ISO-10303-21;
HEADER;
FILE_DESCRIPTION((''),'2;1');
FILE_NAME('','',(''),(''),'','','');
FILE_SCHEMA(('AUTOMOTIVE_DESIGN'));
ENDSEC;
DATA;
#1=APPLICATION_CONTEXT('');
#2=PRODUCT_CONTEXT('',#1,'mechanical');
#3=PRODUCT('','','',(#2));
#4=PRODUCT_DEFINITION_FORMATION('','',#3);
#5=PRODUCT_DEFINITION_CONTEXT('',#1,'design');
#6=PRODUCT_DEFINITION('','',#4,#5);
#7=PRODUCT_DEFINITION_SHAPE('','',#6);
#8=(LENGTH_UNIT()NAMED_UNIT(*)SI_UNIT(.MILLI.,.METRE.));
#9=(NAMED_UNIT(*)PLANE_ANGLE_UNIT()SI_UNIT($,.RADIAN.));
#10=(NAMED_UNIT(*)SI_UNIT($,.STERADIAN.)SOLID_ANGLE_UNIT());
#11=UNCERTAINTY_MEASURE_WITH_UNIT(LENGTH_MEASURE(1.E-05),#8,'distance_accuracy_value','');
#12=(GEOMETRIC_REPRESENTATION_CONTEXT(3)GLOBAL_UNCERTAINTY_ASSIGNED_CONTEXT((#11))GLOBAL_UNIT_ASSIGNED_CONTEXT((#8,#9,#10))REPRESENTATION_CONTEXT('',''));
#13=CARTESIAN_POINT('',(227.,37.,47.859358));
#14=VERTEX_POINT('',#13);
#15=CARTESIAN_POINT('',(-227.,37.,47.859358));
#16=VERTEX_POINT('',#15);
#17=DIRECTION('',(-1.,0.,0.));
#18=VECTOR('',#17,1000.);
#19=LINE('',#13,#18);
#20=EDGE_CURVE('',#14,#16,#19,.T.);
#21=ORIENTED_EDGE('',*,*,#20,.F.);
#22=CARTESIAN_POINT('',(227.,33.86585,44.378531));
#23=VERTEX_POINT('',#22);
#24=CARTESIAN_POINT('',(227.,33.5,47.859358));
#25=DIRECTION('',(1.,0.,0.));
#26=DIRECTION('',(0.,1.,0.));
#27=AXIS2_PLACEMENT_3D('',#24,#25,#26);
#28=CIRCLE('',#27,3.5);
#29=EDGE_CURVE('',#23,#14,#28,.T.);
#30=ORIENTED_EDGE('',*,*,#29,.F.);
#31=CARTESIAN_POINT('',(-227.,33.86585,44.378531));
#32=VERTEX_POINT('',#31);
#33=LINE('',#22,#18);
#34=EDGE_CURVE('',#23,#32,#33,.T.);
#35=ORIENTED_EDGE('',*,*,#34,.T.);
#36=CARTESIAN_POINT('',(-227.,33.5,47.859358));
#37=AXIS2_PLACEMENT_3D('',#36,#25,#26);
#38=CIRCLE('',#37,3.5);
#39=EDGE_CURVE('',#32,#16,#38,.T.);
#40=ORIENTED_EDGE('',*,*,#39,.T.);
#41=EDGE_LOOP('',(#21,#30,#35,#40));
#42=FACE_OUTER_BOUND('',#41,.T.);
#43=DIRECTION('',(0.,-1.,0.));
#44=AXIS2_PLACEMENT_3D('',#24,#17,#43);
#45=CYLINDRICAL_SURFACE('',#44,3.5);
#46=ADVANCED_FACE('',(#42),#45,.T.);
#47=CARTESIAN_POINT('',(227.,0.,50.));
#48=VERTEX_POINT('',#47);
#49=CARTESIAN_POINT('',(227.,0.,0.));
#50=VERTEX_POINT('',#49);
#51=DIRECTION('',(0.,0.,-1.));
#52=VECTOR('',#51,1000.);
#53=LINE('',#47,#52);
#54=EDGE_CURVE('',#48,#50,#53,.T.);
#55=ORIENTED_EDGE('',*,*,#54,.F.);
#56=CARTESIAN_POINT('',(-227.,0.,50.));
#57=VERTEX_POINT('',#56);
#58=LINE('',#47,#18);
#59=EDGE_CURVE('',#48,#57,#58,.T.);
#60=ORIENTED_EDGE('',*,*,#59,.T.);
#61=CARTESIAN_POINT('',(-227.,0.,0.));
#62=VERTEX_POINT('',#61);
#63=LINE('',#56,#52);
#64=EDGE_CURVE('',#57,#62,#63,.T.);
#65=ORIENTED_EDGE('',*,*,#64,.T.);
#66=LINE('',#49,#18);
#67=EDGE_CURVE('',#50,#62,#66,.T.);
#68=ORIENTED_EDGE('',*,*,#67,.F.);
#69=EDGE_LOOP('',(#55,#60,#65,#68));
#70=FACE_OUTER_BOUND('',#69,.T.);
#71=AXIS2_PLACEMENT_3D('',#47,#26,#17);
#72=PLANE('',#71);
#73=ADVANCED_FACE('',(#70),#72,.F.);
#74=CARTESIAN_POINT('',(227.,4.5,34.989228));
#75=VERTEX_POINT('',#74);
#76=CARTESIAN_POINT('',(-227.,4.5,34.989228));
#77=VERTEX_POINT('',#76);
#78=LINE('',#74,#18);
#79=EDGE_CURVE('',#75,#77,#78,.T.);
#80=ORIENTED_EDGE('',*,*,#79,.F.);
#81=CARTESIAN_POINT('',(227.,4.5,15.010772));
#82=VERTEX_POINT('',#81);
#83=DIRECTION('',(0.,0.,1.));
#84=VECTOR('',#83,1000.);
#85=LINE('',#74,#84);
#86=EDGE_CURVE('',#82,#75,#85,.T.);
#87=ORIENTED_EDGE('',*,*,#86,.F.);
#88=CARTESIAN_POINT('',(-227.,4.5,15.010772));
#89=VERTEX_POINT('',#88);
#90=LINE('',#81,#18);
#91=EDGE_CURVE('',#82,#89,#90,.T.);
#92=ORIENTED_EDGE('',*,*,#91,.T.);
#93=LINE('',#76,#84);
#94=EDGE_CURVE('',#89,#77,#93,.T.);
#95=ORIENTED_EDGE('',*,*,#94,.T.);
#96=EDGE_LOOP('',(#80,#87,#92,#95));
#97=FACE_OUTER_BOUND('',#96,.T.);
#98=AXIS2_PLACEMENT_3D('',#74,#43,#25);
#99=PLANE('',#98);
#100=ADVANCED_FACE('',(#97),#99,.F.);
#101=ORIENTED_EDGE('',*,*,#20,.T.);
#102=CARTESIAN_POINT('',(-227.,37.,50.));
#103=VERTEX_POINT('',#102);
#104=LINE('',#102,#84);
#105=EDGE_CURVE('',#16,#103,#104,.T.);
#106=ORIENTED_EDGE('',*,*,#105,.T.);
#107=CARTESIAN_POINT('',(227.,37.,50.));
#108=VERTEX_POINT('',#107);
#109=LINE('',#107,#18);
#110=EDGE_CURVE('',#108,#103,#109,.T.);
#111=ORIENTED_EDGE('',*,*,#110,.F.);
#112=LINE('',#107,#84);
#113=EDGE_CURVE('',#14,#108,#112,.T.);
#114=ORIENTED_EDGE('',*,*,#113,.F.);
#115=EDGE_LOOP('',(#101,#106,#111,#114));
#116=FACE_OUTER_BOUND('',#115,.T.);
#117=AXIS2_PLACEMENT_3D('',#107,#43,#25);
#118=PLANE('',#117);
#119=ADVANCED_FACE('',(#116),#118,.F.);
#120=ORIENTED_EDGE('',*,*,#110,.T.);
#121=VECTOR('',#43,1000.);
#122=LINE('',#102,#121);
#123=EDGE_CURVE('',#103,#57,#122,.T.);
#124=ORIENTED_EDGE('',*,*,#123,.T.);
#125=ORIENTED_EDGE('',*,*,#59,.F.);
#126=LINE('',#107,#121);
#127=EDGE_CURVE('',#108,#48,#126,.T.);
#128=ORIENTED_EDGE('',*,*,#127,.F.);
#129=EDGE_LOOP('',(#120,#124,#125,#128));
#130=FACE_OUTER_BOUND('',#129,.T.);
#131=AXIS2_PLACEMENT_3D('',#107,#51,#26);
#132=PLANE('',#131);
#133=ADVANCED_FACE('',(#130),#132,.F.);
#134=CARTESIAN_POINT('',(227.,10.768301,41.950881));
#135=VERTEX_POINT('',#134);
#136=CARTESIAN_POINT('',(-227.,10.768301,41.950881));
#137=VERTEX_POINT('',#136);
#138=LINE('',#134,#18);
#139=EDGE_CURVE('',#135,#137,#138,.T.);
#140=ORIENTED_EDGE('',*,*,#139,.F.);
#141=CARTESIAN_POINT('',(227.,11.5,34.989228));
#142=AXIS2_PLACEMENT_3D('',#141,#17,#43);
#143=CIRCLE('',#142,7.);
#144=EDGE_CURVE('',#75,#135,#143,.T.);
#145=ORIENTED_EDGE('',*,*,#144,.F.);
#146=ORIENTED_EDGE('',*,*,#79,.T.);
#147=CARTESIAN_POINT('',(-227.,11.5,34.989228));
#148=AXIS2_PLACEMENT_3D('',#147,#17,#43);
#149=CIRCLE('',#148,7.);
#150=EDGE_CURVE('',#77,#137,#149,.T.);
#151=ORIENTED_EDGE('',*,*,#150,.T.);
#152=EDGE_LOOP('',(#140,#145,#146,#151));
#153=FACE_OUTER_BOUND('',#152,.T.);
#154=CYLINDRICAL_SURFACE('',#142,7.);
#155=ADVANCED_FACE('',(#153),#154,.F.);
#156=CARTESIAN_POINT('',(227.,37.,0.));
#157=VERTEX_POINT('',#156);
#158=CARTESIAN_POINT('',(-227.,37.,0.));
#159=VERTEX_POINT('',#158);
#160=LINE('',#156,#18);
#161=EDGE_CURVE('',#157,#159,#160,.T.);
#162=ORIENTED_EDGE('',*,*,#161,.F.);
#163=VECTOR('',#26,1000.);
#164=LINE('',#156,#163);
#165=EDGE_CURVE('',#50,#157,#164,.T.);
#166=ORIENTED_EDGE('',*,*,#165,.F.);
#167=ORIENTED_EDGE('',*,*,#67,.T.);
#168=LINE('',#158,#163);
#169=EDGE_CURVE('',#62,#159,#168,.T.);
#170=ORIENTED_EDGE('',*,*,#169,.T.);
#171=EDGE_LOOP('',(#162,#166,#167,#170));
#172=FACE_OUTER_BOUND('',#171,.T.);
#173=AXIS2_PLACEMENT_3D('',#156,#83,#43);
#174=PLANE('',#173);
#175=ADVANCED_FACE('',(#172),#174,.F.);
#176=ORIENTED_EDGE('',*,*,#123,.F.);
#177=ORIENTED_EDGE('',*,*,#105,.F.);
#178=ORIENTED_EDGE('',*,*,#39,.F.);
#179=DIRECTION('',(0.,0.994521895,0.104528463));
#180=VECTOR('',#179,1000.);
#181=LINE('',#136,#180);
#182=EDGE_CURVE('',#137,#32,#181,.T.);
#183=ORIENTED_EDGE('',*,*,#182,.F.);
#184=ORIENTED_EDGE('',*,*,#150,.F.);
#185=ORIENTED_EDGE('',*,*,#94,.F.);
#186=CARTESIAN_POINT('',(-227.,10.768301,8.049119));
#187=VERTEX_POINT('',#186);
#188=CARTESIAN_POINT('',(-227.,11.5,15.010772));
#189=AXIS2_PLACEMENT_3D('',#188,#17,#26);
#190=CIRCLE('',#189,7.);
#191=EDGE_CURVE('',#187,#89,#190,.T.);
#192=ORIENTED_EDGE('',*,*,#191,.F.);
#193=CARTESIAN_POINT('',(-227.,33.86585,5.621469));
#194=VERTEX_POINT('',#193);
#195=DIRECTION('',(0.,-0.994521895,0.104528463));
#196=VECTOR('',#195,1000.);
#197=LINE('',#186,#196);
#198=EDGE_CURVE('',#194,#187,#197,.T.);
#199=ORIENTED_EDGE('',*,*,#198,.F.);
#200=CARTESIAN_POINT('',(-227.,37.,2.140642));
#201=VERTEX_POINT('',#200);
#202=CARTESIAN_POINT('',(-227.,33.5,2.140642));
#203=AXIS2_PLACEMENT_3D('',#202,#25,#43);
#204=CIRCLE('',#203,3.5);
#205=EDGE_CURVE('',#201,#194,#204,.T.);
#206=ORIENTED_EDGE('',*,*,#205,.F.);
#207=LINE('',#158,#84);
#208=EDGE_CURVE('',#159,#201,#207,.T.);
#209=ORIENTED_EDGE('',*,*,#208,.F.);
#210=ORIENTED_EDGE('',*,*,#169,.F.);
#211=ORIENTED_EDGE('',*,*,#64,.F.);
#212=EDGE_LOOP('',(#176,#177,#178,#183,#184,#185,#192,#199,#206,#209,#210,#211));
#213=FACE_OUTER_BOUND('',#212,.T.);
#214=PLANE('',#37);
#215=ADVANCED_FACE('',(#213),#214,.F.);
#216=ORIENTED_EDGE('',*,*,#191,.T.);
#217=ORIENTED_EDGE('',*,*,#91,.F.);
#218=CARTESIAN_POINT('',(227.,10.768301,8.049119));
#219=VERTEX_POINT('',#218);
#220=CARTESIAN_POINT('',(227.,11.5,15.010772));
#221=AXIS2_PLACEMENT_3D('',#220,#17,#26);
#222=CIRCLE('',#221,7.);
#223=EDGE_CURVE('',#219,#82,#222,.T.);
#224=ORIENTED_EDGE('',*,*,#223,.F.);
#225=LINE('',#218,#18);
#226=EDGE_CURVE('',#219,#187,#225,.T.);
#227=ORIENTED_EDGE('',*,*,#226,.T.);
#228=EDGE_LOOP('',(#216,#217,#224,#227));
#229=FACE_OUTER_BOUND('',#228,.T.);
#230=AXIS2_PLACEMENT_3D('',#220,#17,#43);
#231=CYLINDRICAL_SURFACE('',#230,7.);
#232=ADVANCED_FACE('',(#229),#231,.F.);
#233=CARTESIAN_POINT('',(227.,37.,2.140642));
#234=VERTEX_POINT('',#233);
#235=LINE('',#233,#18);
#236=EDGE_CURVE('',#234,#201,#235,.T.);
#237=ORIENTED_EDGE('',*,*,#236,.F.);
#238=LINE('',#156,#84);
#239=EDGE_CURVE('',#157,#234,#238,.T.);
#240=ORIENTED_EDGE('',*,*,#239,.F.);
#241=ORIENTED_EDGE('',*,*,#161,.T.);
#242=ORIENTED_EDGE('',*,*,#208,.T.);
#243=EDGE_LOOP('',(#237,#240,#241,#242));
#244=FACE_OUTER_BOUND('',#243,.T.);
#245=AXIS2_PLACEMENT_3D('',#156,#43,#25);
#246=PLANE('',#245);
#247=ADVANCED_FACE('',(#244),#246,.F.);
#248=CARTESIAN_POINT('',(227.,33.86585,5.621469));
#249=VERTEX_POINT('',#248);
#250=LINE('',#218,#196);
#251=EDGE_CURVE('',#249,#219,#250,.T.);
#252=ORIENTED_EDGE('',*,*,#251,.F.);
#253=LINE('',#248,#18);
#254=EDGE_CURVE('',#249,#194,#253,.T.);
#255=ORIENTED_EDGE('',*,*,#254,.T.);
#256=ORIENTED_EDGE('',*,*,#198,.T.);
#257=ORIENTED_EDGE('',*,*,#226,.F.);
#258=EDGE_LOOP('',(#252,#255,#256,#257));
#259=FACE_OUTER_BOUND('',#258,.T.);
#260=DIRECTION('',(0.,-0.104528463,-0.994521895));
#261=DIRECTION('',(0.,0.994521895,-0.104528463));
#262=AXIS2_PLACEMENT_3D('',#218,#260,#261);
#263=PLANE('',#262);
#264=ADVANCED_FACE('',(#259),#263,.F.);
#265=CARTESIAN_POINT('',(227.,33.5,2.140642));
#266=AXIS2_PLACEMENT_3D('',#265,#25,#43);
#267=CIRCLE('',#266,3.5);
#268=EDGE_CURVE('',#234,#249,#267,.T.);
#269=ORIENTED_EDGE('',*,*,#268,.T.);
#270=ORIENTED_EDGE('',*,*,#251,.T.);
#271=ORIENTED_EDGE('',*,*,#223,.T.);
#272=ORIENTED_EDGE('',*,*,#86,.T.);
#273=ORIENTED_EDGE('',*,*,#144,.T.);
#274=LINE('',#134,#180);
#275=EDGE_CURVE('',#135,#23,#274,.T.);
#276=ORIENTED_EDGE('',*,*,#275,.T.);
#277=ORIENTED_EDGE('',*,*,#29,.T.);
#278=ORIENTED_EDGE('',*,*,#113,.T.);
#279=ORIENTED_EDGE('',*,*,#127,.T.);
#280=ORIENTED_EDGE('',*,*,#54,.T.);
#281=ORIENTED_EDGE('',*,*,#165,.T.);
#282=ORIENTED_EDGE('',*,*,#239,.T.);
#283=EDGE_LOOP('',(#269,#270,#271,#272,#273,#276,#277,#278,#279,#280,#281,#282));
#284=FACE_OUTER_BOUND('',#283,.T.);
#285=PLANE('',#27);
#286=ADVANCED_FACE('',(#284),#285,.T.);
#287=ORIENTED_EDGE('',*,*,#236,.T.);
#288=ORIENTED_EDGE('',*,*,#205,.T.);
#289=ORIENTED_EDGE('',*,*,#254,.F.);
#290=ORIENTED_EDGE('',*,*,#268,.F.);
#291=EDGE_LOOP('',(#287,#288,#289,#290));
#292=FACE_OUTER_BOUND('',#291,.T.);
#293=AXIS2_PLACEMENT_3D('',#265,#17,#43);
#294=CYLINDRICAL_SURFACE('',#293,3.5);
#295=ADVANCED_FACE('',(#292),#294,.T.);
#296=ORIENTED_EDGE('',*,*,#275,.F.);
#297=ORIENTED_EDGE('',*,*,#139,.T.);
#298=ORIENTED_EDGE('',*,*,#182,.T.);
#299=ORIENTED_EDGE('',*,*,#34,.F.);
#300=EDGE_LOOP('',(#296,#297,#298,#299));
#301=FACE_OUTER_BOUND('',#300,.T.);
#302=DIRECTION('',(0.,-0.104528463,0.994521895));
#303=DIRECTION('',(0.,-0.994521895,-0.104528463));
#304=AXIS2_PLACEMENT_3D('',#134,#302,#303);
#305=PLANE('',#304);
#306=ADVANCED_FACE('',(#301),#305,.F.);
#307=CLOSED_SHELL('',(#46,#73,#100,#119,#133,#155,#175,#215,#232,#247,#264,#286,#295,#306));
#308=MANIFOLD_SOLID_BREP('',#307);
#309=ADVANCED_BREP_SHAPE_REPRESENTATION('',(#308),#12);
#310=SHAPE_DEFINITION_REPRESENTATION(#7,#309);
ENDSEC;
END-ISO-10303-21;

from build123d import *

# Parameters (mm, degrees)
GB_T_707_1988_HOT_ROLLED_CHANNEL_05_1_DEPTH = 454


with BuildPart() as part:
    # Sketch1 → GB/T 707-1988 hot-rolled channel 05(1) (new body)
    with BuildSketch(Plane.YZ.offset(-227)):
        with BuildLine():
            Line((37, 50), (0, 50))
            Line((0, 50), (0, 0))
            Line((0, 0), (37, 0))
            Line((37, 0), (37, 2.140642022))
            ThreePointArc((37, 2.140642022), (36.101006889, 4.482599144), (33.865849621, 5.621468656))
            Line((33.865849621, 5.621468656), (10.768300757, 8.049118866))
            ThreePointArc((10.768300757, 8.049118866), (6.297986222, 10.326857889), (4.5, 15.010772133))
            Line((4.5, 15.010772133), (4.5, 34.989227867))
            ThreePointArc((4.5, 34.989227867), (6.297986222, 39.673142111), (10.768300757, 41.950881134))
            Line((10.768300757, 41.950881134), (33.865849621, 44.378531344))
            ThreePointArc((33.865849621, 44.378531344), (36.101006889, 45.517400856), (37, 47.859357978))
            Line((37, 47.859357978), (37, 50))
        make_face()
    extrude(amount=GB_T_707_1988_HOT_ROLLED_CHANNEL_05_1_DEPTH)


solid = part.part
